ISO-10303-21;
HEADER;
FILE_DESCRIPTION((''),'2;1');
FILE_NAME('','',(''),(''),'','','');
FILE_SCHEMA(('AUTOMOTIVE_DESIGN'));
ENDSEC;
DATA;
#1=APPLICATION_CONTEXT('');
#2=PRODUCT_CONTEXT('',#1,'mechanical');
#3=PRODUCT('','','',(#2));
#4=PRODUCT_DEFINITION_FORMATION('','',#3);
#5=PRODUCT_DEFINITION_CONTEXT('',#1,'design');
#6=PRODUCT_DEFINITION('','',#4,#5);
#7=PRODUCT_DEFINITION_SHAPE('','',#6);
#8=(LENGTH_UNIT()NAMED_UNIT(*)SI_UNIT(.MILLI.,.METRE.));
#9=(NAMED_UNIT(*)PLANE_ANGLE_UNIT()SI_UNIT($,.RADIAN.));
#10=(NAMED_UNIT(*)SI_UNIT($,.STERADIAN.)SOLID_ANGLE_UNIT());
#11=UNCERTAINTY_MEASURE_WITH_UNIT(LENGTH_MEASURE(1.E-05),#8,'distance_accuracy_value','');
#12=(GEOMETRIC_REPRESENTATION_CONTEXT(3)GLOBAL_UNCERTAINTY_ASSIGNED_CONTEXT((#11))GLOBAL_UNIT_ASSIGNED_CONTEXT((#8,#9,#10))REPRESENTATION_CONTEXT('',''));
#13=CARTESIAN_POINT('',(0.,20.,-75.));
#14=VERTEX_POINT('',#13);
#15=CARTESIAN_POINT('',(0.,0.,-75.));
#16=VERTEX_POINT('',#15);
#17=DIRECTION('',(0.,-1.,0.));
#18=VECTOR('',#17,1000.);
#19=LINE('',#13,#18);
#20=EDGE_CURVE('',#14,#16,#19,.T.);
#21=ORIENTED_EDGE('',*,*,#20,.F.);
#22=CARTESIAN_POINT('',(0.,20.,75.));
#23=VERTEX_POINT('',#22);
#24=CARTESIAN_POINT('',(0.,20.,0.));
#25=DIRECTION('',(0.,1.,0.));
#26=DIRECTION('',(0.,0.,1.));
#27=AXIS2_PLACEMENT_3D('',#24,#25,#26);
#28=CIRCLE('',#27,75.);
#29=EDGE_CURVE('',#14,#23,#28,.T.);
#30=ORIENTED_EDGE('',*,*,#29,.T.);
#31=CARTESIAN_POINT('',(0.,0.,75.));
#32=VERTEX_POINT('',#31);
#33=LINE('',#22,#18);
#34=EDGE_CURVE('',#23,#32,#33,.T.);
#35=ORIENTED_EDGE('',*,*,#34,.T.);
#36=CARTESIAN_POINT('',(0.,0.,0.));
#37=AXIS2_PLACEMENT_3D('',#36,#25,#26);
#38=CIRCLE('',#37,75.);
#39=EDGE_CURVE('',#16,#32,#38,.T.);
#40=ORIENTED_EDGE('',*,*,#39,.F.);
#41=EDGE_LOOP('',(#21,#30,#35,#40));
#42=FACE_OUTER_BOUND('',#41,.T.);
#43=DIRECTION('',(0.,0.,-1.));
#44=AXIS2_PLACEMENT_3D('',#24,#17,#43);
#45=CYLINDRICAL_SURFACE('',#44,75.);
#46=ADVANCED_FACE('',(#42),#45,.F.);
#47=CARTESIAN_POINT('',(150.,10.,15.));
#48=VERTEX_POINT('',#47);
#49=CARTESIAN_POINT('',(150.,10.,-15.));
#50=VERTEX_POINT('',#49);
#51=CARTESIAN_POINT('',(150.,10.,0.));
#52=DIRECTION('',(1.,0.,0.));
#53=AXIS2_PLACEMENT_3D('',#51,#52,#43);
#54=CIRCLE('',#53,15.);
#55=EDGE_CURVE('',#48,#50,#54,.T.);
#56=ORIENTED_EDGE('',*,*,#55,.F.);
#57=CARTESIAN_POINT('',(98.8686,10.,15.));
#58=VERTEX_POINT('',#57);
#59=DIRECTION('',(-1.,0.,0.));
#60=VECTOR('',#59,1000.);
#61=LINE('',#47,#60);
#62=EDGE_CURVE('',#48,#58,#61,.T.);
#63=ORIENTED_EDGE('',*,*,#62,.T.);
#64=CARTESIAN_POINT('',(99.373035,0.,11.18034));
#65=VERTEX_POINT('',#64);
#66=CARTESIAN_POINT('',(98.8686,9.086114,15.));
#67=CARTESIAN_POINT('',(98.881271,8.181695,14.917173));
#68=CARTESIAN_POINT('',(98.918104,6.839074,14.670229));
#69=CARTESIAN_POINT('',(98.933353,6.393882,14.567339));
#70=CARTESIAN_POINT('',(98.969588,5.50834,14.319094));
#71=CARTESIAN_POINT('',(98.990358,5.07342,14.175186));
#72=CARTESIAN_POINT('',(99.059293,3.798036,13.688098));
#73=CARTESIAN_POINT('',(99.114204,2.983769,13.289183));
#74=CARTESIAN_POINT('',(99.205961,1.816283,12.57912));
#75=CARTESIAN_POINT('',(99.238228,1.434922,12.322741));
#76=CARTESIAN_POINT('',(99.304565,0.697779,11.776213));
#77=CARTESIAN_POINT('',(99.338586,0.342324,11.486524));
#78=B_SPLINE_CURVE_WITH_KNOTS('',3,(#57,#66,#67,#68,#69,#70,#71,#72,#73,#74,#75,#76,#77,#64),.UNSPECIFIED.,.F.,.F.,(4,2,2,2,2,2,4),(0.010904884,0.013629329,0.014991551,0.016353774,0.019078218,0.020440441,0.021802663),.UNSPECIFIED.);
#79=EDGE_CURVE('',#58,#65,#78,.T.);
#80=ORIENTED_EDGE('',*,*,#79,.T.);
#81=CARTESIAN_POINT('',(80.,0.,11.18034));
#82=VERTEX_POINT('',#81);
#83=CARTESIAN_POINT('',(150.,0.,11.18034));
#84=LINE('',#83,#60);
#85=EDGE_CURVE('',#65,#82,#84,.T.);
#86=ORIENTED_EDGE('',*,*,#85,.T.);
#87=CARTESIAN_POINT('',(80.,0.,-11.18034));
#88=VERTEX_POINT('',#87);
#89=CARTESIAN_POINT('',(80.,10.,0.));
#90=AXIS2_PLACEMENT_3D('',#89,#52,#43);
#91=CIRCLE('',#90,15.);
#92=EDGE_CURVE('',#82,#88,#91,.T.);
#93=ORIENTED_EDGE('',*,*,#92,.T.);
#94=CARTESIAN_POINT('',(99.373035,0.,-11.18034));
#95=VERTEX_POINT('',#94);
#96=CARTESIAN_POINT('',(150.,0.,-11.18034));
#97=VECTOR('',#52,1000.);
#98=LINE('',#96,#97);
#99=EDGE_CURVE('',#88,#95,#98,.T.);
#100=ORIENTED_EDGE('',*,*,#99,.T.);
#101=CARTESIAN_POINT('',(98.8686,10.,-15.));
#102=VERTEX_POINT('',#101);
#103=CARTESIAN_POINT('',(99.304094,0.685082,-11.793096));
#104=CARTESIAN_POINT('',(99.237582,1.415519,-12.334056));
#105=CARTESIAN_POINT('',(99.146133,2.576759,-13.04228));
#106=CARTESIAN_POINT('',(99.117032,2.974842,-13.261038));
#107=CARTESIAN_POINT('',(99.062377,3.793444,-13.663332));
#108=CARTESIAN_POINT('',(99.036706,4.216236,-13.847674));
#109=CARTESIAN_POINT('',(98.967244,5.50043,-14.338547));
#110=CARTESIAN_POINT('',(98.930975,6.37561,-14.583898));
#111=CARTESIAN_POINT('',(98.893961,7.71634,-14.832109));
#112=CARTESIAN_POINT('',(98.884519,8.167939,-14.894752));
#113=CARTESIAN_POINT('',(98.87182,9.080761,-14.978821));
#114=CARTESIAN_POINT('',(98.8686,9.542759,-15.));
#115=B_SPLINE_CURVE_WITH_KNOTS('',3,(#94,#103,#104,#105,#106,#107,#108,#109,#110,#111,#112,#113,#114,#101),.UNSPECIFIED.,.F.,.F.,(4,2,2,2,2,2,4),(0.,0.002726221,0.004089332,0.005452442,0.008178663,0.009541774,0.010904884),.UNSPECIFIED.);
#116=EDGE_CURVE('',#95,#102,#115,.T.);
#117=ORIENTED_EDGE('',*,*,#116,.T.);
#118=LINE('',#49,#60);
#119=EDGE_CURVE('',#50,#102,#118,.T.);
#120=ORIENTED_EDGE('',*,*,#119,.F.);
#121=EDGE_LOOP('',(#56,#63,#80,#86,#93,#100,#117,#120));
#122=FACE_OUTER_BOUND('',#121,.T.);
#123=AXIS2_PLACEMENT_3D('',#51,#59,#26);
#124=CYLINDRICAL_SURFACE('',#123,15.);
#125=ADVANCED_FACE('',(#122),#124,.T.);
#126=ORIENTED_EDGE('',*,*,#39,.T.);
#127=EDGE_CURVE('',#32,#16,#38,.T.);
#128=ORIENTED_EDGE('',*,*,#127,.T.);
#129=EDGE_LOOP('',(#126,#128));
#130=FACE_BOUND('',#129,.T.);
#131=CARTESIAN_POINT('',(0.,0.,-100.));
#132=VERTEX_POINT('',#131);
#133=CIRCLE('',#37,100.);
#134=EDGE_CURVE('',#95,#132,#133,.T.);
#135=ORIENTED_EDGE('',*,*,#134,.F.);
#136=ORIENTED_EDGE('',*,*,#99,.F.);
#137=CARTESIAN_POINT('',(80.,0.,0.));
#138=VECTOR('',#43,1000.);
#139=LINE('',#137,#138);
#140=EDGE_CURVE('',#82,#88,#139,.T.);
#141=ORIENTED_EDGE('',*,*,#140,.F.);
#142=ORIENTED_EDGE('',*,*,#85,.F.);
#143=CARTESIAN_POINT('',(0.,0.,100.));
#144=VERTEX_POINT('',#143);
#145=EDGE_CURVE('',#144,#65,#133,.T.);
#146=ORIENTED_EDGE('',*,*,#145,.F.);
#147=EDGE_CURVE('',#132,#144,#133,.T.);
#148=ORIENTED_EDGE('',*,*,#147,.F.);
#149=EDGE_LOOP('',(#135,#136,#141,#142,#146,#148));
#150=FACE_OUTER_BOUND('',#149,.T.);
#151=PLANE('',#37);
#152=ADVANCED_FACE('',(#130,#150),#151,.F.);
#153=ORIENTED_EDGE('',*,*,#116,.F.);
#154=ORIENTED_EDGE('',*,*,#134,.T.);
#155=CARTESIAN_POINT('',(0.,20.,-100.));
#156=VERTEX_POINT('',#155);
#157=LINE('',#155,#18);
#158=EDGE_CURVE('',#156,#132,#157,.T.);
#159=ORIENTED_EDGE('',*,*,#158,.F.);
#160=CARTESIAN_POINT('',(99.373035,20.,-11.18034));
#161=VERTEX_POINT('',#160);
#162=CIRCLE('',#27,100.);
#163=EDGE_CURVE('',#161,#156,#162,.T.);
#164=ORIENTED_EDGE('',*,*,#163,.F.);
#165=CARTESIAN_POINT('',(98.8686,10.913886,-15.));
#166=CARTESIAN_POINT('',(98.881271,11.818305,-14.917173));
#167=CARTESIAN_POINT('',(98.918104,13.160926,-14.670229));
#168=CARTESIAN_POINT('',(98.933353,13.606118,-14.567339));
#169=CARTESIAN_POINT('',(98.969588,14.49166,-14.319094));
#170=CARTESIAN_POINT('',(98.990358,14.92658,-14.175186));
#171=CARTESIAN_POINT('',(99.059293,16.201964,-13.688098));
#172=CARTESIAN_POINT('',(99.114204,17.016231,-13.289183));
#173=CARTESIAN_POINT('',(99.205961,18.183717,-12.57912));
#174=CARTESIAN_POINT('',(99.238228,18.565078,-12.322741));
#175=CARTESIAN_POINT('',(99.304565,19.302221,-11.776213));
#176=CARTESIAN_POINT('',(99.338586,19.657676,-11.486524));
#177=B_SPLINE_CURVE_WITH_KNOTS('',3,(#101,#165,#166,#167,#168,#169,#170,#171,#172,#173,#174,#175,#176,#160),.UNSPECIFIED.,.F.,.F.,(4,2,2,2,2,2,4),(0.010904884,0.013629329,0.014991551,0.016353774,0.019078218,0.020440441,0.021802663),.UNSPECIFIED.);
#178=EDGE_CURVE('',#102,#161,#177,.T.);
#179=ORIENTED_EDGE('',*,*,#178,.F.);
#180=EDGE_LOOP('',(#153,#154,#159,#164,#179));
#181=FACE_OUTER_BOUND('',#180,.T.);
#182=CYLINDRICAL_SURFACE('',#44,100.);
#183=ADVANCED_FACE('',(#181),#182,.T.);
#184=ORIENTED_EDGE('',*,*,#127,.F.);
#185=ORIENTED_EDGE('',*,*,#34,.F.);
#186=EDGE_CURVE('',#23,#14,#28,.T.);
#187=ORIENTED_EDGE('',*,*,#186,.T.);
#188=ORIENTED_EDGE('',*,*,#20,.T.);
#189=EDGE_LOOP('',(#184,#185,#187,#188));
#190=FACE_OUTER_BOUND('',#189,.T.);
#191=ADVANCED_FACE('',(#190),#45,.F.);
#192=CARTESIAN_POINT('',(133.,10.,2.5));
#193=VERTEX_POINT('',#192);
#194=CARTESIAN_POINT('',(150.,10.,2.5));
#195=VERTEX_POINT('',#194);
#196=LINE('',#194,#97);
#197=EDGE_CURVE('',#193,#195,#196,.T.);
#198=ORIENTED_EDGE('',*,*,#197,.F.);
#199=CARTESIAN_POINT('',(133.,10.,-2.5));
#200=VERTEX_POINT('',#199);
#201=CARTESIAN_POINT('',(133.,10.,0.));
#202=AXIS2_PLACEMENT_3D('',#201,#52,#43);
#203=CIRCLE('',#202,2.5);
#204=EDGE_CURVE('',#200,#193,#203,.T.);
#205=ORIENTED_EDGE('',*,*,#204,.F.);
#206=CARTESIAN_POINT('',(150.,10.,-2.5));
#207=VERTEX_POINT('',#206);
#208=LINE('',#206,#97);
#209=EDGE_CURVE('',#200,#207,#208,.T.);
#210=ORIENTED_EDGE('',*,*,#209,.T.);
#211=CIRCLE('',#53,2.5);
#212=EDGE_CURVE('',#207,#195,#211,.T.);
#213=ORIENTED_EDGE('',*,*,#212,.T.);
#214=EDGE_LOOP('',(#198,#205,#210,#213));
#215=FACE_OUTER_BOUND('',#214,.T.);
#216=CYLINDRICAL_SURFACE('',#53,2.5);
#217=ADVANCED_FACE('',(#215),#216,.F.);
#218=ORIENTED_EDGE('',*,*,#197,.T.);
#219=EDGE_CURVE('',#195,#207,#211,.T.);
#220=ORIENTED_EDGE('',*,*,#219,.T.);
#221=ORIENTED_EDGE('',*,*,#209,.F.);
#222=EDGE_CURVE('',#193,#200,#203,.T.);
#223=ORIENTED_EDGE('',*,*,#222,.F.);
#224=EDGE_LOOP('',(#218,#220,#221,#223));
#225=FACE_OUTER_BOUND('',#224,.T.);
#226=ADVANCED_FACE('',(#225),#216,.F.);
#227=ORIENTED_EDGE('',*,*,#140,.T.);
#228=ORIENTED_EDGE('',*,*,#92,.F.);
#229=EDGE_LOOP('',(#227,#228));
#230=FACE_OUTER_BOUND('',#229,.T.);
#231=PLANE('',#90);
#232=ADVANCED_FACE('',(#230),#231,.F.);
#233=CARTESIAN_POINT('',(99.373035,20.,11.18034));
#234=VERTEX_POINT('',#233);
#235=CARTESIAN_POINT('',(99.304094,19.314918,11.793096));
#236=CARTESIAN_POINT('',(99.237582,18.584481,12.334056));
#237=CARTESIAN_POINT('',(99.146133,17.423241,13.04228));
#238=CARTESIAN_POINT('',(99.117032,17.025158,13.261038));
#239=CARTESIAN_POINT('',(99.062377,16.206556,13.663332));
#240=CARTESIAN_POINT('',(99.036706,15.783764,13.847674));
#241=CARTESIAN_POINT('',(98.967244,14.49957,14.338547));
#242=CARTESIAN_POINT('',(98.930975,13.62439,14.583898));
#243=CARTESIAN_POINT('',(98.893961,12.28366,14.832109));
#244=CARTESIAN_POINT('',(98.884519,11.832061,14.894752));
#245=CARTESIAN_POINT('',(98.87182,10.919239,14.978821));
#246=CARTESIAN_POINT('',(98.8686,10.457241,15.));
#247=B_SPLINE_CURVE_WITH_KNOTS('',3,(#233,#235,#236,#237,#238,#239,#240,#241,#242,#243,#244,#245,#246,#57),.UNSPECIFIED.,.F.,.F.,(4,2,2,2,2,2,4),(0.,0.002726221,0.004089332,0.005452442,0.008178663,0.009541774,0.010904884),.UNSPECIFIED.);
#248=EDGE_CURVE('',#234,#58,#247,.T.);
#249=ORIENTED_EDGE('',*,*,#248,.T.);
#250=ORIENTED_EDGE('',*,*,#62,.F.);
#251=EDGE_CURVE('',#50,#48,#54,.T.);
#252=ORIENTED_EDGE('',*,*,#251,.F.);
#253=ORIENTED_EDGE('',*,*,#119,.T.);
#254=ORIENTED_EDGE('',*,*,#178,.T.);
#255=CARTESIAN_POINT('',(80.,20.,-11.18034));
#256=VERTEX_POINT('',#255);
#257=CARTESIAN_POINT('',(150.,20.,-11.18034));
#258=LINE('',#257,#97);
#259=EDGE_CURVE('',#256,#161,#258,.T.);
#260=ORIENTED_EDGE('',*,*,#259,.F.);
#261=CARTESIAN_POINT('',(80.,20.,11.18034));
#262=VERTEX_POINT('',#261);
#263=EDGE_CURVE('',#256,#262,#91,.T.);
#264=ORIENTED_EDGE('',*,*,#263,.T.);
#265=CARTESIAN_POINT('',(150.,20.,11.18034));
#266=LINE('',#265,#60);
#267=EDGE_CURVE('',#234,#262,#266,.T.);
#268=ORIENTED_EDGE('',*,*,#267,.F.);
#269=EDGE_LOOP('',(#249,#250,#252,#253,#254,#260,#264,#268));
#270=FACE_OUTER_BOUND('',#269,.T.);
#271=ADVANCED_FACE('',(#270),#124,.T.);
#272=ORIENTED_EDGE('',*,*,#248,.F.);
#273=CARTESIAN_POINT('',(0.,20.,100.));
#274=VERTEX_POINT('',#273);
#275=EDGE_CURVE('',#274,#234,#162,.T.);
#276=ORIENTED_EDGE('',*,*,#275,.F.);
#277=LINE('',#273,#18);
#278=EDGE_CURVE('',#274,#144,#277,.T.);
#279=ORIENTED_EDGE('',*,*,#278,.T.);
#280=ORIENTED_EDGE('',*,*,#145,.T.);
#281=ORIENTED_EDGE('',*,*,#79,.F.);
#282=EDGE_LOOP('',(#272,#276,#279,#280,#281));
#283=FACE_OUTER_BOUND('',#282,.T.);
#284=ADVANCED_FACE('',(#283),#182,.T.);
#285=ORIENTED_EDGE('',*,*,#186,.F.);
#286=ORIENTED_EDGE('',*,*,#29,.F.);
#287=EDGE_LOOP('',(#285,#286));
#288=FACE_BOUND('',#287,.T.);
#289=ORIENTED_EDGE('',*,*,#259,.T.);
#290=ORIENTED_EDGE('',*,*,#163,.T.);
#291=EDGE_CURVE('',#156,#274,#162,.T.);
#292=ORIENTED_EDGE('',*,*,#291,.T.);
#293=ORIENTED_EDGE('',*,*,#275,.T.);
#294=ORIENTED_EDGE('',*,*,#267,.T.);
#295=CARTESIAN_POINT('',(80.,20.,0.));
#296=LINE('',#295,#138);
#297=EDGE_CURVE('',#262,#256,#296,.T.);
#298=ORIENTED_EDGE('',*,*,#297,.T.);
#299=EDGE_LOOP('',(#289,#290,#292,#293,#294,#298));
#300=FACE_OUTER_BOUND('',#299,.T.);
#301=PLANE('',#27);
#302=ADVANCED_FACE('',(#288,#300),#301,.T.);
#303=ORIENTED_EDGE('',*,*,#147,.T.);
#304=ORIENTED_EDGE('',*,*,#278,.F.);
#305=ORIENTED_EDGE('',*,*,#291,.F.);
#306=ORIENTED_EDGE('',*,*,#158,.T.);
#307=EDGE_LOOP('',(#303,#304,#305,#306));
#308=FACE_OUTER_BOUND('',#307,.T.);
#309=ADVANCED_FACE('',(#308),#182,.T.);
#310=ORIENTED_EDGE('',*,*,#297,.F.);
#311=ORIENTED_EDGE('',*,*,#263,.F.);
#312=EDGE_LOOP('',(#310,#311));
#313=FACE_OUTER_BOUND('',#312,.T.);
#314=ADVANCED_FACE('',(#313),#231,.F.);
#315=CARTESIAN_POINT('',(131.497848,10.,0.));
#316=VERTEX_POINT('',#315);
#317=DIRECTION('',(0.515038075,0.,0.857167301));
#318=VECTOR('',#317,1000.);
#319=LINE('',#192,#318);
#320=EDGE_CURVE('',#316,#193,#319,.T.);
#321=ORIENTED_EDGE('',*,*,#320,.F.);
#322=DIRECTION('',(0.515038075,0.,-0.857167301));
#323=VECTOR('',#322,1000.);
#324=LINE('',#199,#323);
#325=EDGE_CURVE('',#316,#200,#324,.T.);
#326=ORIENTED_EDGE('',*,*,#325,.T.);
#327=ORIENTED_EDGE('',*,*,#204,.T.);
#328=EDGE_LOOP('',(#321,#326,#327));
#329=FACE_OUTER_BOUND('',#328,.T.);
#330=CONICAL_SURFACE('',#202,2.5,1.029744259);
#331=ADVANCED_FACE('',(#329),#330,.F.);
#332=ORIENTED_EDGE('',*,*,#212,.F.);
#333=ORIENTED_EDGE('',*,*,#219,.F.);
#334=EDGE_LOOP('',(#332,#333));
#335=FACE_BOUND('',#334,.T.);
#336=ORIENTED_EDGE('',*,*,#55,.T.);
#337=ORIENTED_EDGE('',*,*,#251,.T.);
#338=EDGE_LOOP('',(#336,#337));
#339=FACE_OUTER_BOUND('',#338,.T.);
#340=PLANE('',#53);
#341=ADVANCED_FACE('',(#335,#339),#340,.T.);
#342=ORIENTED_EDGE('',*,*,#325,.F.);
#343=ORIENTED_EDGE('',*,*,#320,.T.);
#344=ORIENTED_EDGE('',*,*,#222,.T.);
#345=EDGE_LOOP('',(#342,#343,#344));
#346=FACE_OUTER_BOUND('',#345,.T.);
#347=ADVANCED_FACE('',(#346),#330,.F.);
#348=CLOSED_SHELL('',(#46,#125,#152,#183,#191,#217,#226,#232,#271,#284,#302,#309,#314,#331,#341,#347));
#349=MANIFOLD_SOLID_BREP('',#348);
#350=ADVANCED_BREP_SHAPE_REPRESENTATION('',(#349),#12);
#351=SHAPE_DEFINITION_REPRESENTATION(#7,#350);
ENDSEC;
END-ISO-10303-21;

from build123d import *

# Parameters (mm, degrees)
SKETCH1_R             = 100
SKETCH1_R_2           = 75
BOSS_EXTRUDE1_DEPTH   = 20
BOSS_EXTRUDE2_START   = 80
SKETCH2_R             = 15
BOSS_EXTRUDE2_DEPTH   = 70
M6_TAPPED_HOLE1_D     = 5
M6_TAPPED_HOLE1_DEPTH = 17
M6_TAPPED_HOLE1_TIP   = 1.502151548


with BuildPart() as part:
    # Sketch1 → Boss-Extrude1 (new body)
    with BuildSketch(Plane(origin=(0, 0, 0), x_dir=(1, 0, 0), z_dir=(0, 1, 0))):
        with Locations(Location((0, 0, 0), (0, 0, 270))):
            Circle(SKETCH1_R)
        with Locations(Location((0, 0, 0), (0, 0, 270))):
            Circle(SKETCH1_R_2, mode=Mode.SUBTRACT)
    extrude(amount=BOSS_EXTRUDE1_DEPTH)

    # Sketch2 → Boss-Extrude2 (add)
    with BuildSketch(Plane(origin=(0, 0, 0), x_dir=(0, 0, -1), z_dir=(1, 0, 0)).offset(BOSS_EXTRUDE2_START)):
        with Locations(Location((0, 10, 0), (0, 0, 138.189685104))):
            Circle(SKETCH2_R)
    extrude(amount=BOSS_EXTRUDE2_DEPTH)

    # M6 Tapped Hole1
    with Locations(Plane(origin=(150, 0, 0), x_dir=(0, 0, -1), z_dir=(1, 0, 0))):
        with Locations((0, 10)):
            Hole(M6_TAPPED_HOLE1_D / 2, depth=M6_TAPPED_HOLE1_DEPTH)
            with Locations((0, 0, -(M6_TAPPED_HOLE1_DEPTH + M6_TAPPED_HOLE1_TIP / 2))):  # 118° drill point
                Cone(0, M6_TAPPED_HOLE1_D / 2, M6_TAPPED_HOLE1_TIP, mode=Mode.SUBTRACT)


solid = part.part
